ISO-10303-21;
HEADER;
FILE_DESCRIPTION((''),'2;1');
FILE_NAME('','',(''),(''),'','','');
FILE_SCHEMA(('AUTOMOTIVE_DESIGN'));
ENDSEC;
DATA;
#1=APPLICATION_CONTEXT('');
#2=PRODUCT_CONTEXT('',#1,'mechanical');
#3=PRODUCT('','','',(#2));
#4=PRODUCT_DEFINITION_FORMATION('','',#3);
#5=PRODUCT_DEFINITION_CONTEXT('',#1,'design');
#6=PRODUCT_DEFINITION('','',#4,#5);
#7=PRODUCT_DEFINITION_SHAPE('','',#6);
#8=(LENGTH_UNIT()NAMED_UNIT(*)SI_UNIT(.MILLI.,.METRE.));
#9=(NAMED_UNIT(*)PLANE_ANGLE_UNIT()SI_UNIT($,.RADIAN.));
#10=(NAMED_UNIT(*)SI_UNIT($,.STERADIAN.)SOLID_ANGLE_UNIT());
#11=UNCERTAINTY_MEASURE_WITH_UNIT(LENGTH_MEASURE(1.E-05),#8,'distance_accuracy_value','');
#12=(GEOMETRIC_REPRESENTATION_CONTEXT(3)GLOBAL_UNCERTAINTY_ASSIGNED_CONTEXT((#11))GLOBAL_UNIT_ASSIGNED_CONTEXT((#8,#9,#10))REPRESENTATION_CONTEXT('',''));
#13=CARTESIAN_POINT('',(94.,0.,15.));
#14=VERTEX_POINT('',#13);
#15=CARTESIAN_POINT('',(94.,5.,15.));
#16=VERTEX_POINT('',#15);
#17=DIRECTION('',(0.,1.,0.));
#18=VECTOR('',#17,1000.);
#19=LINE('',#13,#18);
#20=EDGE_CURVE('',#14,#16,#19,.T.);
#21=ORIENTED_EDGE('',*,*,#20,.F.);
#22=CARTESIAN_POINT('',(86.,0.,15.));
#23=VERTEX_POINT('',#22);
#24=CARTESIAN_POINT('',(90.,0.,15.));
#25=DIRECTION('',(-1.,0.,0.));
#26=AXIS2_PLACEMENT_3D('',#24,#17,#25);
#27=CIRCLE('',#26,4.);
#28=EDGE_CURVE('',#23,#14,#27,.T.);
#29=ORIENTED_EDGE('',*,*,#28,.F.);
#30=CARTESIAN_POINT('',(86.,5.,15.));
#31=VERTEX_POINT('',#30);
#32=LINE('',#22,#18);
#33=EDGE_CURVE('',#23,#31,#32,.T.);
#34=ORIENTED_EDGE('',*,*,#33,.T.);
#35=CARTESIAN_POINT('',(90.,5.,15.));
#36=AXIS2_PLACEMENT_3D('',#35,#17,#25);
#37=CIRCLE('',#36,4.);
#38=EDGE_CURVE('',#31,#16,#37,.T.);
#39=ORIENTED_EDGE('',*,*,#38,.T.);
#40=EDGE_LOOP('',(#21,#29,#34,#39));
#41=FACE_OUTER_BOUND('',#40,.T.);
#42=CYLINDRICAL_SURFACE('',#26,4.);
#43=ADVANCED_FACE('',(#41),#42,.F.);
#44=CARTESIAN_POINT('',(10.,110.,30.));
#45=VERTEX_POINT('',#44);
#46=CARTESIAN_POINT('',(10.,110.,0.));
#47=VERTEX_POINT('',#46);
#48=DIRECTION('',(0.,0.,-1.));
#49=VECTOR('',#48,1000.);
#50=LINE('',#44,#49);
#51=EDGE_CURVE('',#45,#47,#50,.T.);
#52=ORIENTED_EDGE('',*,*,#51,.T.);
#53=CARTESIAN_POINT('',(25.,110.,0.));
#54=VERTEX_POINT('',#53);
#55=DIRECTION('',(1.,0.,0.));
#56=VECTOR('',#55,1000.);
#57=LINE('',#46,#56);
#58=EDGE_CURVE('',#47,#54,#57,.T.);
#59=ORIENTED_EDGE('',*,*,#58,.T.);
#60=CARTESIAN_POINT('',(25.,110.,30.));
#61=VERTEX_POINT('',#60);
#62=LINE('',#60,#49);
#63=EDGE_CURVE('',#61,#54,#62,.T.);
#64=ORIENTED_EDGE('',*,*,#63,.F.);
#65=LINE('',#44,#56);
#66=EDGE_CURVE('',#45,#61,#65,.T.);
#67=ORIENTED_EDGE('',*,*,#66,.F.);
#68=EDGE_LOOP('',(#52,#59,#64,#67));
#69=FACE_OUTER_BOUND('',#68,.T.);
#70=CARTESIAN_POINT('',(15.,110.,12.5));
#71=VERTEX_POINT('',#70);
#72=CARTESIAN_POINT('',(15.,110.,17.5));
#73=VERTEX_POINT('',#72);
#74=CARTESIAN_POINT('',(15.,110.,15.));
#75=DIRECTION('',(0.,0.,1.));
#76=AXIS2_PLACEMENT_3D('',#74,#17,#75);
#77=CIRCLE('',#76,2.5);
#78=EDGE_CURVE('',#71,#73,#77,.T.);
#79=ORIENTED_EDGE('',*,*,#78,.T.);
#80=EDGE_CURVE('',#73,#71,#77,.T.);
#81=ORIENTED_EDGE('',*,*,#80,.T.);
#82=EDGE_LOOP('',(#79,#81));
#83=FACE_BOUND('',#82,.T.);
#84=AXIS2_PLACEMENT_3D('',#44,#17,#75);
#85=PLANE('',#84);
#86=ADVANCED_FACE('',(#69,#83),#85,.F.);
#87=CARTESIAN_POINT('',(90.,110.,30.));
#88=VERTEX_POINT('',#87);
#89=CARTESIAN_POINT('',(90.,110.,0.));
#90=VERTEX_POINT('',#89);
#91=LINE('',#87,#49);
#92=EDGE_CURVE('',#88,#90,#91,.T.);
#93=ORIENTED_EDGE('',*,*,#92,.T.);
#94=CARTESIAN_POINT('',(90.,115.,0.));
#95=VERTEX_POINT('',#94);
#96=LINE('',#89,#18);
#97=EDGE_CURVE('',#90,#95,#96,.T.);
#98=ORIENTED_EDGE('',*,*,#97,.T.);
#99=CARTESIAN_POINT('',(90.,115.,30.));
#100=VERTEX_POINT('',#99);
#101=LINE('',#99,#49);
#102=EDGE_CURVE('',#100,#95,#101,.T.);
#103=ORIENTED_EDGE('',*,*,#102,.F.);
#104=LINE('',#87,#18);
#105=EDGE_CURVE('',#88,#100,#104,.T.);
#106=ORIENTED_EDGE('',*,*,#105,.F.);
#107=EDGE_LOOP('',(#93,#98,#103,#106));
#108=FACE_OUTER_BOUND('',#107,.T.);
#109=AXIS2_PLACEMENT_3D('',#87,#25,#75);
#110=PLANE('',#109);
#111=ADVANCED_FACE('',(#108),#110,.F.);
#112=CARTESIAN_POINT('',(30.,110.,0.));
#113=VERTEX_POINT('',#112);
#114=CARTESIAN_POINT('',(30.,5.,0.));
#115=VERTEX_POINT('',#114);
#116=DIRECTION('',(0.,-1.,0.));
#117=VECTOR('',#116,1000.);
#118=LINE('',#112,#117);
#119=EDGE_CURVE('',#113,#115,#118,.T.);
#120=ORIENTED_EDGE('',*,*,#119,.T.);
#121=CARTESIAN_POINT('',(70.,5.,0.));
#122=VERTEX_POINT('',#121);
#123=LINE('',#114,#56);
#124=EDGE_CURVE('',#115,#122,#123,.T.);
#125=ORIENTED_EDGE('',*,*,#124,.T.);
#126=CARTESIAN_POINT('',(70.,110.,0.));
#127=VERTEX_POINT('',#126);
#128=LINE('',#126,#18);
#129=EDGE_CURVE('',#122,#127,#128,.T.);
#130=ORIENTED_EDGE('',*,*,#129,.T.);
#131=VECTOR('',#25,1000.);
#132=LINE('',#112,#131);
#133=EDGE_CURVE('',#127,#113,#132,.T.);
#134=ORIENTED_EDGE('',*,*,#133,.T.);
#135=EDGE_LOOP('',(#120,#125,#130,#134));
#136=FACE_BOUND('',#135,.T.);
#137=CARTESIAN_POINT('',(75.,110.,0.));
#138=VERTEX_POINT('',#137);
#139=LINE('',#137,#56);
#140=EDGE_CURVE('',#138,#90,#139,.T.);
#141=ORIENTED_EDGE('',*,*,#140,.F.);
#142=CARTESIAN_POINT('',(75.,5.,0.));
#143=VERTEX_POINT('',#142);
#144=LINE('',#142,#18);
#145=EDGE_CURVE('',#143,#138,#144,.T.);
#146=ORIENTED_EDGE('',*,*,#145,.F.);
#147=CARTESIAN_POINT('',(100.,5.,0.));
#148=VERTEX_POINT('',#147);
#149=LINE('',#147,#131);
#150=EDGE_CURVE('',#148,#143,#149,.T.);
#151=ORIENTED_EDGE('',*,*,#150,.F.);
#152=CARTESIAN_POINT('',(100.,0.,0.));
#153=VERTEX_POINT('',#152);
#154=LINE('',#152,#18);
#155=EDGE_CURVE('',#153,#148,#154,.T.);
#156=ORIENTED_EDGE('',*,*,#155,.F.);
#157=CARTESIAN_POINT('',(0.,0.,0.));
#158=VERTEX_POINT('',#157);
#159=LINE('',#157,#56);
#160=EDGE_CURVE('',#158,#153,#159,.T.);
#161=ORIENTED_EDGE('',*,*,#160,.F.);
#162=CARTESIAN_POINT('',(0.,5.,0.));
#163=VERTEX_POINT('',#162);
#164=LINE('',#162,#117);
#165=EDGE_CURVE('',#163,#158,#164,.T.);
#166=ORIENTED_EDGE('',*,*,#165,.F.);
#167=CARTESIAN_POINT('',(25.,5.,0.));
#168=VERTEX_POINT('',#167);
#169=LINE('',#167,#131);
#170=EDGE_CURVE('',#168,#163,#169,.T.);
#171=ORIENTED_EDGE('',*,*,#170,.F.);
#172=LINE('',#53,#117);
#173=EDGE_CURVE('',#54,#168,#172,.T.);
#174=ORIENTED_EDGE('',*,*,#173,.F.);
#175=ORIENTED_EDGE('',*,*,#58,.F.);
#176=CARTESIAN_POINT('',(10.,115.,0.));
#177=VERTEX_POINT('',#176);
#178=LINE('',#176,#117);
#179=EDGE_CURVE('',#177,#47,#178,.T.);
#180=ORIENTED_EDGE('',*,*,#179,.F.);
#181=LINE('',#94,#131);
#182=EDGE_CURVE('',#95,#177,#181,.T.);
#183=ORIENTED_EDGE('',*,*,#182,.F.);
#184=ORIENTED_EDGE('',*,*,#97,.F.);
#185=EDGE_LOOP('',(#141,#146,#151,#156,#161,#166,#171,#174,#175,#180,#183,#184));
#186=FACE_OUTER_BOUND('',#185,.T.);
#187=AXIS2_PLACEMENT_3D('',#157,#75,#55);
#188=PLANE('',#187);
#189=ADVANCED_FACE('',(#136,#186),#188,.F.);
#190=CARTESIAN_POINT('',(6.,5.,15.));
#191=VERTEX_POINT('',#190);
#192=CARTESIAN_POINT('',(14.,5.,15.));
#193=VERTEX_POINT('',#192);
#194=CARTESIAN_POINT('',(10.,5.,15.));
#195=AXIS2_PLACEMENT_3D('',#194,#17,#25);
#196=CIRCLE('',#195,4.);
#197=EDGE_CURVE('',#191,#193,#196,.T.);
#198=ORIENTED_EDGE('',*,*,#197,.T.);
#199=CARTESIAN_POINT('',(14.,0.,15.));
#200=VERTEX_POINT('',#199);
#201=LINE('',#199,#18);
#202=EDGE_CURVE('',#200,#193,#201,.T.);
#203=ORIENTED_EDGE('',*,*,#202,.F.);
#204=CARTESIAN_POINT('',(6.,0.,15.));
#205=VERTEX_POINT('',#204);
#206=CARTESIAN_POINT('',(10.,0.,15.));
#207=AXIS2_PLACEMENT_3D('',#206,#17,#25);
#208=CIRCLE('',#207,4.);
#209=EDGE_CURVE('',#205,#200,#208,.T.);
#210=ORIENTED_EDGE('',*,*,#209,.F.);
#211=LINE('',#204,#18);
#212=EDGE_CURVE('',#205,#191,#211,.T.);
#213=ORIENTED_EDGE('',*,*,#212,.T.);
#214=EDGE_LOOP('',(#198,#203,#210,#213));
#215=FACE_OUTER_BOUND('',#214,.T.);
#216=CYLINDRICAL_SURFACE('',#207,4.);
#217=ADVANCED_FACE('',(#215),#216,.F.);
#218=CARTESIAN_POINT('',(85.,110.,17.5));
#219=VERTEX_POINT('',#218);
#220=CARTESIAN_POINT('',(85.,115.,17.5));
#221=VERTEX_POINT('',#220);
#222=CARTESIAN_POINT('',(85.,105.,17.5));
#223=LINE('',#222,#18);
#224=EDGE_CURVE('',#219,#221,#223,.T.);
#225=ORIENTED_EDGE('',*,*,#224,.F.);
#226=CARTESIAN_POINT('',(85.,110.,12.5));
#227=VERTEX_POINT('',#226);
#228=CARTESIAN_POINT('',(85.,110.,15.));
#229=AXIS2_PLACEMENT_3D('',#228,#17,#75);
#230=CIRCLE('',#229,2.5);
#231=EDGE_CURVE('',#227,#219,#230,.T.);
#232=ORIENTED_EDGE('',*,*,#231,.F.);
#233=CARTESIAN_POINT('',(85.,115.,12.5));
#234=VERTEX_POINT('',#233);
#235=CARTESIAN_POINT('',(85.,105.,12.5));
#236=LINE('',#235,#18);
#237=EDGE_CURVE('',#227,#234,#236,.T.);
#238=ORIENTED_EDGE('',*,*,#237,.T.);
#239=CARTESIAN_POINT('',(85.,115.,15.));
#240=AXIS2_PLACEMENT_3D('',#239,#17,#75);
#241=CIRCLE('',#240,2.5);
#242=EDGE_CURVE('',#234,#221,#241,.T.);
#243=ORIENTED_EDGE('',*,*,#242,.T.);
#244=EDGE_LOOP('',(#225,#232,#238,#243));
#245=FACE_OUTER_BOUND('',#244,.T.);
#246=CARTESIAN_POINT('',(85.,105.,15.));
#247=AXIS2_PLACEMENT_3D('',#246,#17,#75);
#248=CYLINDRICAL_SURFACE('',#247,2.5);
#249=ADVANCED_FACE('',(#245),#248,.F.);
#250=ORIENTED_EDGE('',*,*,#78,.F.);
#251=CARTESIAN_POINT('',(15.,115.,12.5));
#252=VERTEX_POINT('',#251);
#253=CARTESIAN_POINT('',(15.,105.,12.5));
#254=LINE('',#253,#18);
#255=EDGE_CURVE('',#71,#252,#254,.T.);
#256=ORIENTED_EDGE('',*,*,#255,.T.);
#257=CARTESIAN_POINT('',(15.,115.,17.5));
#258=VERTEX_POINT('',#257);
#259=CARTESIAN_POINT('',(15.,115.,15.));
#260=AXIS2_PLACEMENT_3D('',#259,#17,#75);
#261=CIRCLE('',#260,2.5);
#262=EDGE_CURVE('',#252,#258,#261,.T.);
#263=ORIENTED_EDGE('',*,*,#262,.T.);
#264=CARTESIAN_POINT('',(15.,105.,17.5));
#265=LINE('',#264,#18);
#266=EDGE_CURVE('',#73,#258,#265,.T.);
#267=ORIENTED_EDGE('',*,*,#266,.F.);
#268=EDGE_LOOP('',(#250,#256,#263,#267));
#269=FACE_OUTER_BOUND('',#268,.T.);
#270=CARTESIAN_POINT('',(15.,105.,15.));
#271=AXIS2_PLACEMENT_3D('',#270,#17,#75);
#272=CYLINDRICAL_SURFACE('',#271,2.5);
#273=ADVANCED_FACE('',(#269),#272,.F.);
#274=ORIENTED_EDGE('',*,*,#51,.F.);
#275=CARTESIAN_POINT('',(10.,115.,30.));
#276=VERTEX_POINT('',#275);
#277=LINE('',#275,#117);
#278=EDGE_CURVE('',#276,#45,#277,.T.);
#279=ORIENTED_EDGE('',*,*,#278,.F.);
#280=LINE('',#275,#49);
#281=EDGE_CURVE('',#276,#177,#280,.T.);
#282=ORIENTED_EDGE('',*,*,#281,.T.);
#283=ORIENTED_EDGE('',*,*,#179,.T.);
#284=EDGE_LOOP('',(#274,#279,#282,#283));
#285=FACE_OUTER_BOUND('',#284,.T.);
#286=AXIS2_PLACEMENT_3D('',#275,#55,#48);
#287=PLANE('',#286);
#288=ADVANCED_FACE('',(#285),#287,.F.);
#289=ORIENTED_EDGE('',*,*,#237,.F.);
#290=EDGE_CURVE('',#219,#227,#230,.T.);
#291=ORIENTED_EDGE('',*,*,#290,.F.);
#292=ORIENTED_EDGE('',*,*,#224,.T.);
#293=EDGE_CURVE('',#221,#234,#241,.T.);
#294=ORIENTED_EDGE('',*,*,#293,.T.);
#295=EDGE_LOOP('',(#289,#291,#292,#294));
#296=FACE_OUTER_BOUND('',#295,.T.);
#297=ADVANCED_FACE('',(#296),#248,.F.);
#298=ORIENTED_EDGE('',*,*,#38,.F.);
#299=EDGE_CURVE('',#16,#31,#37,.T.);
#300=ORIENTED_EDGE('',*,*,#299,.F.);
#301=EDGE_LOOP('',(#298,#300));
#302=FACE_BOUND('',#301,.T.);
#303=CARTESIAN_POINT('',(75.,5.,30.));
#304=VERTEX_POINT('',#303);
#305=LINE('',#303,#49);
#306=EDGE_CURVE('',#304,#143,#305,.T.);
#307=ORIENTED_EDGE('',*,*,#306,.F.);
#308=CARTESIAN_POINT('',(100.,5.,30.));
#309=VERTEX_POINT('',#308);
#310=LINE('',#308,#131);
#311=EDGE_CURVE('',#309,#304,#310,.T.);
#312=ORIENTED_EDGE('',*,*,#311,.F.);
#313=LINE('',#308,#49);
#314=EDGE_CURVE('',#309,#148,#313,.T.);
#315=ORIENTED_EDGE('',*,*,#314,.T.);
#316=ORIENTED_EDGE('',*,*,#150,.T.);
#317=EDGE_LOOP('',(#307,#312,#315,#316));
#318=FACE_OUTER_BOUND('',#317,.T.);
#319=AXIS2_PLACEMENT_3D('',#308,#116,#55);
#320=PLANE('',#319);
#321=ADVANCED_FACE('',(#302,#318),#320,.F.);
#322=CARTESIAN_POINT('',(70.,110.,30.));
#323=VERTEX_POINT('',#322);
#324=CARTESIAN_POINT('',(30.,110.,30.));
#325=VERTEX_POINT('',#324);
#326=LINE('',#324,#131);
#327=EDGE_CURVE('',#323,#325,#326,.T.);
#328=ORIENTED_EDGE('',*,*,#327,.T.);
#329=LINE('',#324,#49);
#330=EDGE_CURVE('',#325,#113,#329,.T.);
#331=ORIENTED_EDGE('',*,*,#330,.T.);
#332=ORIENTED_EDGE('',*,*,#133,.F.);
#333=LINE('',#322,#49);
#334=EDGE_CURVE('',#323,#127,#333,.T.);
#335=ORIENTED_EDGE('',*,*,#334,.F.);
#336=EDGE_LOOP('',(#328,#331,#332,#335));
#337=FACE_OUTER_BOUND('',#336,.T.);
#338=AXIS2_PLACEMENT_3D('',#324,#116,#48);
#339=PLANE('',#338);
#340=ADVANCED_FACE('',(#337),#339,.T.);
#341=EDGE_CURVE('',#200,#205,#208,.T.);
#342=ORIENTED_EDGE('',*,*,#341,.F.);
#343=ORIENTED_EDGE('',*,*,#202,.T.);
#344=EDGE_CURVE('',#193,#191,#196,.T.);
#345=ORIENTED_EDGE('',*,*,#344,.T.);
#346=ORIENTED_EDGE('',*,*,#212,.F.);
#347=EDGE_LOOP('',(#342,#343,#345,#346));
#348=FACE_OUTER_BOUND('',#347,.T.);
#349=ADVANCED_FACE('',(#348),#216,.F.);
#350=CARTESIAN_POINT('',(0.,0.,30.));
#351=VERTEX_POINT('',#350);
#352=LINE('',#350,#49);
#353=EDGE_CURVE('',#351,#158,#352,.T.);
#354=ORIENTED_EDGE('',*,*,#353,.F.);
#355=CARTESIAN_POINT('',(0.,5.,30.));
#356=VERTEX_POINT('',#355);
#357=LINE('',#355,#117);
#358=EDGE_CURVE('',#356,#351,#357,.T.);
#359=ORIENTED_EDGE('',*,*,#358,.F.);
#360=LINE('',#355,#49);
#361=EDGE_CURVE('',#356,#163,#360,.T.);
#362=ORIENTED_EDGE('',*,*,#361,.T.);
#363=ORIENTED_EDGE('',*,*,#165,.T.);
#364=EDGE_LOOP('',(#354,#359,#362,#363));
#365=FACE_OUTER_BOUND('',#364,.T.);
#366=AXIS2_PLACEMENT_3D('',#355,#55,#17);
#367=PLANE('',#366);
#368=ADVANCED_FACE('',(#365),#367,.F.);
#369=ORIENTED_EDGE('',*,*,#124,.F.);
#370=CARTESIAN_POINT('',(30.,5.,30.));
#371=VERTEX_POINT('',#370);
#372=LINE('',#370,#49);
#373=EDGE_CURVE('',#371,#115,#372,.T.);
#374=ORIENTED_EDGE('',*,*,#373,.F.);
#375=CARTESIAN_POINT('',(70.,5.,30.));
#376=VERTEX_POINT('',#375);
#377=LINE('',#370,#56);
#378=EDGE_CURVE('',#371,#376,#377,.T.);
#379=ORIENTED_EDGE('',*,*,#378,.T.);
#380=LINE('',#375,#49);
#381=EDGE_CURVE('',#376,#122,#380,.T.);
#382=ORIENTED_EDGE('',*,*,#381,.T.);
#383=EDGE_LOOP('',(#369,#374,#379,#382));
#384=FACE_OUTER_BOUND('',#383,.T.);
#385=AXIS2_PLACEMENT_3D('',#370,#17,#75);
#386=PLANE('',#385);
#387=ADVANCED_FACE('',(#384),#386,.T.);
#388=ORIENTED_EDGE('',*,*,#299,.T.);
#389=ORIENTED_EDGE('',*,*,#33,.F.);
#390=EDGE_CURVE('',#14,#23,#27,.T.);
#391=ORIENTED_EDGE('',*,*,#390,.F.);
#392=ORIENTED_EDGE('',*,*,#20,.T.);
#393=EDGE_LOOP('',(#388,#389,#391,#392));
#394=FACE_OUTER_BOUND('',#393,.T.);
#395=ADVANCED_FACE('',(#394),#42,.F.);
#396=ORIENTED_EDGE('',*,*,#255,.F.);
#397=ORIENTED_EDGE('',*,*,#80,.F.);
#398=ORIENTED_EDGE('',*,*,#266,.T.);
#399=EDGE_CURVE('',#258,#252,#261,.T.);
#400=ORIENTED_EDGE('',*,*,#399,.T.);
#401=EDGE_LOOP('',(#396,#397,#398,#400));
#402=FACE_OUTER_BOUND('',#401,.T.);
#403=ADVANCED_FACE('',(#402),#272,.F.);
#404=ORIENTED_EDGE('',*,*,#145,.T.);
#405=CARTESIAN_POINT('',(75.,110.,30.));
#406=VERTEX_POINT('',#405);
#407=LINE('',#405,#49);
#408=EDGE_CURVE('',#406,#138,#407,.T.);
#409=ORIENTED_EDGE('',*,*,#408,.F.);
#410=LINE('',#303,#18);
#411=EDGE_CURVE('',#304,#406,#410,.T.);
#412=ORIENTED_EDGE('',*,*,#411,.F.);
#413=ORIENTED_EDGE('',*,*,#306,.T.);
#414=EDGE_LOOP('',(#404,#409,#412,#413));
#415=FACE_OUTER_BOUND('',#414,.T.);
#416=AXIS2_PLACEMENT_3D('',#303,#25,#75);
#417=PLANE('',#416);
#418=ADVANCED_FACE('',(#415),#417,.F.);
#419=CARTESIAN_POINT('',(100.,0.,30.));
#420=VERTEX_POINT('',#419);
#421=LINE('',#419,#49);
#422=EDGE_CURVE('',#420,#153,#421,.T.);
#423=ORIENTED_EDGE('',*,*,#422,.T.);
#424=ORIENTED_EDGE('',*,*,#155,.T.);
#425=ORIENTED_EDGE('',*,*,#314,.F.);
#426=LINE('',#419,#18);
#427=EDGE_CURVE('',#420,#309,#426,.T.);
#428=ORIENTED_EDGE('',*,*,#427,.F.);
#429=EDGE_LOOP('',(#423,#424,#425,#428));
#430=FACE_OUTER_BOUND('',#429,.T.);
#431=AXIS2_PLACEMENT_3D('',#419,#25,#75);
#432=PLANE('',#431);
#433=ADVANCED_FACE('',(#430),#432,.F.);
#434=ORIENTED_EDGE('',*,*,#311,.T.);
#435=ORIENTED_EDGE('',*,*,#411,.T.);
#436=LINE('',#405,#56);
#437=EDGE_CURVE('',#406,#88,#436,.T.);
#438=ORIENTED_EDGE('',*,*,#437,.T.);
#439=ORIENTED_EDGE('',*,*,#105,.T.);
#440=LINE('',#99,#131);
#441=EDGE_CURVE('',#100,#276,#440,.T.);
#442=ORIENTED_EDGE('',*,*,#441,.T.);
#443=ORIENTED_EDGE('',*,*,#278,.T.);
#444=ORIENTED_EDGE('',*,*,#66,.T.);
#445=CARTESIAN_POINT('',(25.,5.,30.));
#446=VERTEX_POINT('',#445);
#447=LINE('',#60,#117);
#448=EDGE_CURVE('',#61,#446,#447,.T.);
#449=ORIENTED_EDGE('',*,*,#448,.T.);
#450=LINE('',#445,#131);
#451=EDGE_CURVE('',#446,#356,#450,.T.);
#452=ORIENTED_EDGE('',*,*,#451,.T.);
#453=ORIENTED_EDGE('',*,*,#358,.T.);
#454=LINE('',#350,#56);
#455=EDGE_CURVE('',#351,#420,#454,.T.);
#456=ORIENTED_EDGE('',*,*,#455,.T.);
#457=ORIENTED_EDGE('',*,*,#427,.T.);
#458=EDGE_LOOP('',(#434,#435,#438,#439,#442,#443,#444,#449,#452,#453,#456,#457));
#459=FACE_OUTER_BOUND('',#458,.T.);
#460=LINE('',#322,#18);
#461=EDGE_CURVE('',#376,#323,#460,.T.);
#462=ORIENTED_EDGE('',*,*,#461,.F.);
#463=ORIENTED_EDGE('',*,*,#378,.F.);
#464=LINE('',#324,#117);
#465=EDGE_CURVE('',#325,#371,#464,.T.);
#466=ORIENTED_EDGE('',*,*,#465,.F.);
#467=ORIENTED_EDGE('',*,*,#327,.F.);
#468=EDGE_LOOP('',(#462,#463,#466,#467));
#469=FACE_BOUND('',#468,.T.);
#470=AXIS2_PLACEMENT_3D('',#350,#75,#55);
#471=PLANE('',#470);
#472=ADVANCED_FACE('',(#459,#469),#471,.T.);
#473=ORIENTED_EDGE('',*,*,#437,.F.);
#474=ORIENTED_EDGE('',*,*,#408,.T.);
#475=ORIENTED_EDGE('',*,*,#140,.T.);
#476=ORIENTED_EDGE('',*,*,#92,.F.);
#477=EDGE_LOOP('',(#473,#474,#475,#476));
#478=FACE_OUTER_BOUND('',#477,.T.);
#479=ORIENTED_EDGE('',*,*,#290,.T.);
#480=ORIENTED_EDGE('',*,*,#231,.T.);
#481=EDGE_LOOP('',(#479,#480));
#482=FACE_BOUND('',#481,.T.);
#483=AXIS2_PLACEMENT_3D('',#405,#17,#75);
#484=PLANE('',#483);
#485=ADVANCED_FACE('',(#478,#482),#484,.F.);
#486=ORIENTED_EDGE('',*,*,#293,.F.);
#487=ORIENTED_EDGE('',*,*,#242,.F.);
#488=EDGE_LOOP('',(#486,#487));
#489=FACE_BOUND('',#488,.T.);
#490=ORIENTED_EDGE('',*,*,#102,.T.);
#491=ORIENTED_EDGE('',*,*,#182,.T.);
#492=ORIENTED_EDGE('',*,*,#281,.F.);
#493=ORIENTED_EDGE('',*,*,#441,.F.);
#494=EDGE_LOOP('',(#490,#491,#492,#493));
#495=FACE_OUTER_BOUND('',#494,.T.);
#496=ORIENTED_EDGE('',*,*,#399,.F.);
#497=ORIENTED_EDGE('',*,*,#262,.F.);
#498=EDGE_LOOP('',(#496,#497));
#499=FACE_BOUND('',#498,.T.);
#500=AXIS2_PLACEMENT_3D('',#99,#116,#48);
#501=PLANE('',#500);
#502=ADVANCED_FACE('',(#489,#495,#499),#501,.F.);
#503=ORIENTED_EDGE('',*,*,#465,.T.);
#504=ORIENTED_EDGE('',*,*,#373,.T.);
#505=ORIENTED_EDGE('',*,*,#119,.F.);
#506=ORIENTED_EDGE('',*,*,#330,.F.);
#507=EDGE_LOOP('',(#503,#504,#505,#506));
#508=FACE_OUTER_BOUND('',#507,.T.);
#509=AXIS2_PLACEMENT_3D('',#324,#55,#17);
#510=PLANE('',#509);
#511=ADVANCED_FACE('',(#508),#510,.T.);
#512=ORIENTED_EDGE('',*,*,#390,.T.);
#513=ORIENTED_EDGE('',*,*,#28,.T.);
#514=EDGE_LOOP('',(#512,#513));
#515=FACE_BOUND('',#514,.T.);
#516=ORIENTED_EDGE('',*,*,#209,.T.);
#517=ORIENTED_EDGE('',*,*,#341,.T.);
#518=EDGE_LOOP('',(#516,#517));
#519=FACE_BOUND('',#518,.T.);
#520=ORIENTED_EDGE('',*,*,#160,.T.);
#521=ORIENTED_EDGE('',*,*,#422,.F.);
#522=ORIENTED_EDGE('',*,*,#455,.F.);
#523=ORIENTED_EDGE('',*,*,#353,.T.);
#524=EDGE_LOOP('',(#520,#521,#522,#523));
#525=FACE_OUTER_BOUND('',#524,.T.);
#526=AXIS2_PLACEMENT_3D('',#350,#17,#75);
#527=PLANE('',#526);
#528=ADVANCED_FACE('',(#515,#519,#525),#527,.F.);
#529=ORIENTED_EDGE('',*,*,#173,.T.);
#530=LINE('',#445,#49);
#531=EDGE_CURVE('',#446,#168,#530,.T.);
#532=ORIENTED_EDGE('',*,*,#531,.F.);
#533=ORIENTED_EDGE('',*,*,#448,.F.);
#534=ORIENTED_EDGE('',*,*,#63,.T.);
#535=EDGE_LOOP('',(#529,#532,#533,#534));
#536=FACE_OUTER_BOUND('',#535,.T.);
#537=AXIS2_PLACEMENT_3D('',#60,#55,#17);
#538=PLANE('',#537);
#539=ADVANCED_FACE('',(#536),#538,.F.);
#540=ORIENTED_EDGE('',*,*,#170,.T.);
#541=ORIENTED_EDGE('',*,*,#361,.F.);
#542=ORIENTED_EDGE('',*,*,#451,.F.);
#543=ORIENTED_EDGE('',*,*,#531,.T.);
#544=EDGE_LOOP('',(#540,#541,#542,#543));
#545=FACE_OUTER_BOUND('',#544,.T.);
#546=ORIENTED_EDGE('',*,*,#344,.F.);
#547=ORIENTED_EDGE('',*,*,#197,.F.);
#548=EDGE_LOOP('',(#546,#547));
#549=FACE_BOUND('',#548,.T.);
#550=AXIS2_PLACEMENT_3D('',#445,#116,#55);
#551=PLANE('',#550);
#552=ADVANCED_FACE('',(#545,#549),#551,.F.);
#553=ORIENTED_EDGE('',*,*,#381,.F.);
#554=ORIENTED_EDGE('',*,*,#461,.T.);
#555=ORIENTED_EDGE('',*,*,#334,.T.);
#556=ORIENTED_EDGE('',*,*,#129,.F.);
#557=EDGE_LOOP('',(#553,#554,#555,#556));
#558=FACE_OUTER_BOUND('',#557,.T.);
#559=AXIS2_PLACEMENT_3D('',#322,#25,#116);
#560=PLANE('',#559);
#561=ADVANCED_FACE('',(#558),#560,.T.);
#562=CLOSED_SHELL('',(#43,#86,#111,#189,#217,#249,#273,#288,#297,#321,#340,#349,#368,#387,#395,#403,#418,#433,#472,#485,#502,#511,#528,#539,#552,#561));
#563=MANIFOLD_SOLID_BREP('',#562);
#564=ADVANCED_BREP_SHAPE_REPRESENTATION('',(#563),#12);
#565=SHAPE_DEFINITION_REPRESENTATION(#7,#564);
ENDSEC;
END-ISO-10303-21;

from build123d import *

# Parameters (mm, degrees)
SKETCH1_W           = 40
SKETCH1_H           = 105
BOSS_EXTRUDE1_DEPTH = 30
SKETCH2_R           = 4
CUT_EXTRUDE1_DEPTH  = 152.657508881
SKETCH3_R           = 2.5
CUT_EXTRUDE2_DEPTH  = 10


with BuildPart() as part:
    # Sketch1 → Boss-Extrude1 (new body)
    with BuildSketch(Plane.XY):
        Polygon((0, 0), (100, 0), (100, 5), (75, 5), (75, 110), (90, 110), (90, 115), (10, 115), (10, 110), (25, 110), (25, 5), (0, 5), align=None)
        with Locations((50, 57.5)):
            Rectangle(SKETCH1_W, SKETCH1_H, mode=Mode.SUBTRACT)
    extrude(amount=BOSS_EXTRUDE1_DEPTH)

    # Sketch2 → Cut-Extrude1 (cut, through all)
    with BuildSketch(Plane(origin=(0, 5, 0), x_dir=(1, 0, 0), z_dir=(0, 1, 0))):
        with Locations(Location((90, -15, 0), (0, 0, 180))):
            Circle(SKETCH2_R)
        with Locations(Location((10, -15, 0), (0, 0, 180))):
            Circle(SKETCH2_R)
    extrude(amount=-CUT_EXTRUDE1_DEPTH, mode=Mode.SUBTRACT)

    # Sketch3 → Cut-Extrude2 (cut)
    with BuildSketch(Plane(origin=(0, 115, 0), x_dir=(1, 0, 0), z_dir=(0, 1, 0))):
        with Locations(Location((15, -15, 0), (0, 0, 270))):
            Circle(SKETCH3_R)
        with Locations(Location((85, -15, 0), (0, 0, 270))):
            Circle(SKETCH3_R)
    extrude(amount=-CUT_EXTRUDE2_DEPTH, mode=Mode.SUBTRACT)


solid = part.part
